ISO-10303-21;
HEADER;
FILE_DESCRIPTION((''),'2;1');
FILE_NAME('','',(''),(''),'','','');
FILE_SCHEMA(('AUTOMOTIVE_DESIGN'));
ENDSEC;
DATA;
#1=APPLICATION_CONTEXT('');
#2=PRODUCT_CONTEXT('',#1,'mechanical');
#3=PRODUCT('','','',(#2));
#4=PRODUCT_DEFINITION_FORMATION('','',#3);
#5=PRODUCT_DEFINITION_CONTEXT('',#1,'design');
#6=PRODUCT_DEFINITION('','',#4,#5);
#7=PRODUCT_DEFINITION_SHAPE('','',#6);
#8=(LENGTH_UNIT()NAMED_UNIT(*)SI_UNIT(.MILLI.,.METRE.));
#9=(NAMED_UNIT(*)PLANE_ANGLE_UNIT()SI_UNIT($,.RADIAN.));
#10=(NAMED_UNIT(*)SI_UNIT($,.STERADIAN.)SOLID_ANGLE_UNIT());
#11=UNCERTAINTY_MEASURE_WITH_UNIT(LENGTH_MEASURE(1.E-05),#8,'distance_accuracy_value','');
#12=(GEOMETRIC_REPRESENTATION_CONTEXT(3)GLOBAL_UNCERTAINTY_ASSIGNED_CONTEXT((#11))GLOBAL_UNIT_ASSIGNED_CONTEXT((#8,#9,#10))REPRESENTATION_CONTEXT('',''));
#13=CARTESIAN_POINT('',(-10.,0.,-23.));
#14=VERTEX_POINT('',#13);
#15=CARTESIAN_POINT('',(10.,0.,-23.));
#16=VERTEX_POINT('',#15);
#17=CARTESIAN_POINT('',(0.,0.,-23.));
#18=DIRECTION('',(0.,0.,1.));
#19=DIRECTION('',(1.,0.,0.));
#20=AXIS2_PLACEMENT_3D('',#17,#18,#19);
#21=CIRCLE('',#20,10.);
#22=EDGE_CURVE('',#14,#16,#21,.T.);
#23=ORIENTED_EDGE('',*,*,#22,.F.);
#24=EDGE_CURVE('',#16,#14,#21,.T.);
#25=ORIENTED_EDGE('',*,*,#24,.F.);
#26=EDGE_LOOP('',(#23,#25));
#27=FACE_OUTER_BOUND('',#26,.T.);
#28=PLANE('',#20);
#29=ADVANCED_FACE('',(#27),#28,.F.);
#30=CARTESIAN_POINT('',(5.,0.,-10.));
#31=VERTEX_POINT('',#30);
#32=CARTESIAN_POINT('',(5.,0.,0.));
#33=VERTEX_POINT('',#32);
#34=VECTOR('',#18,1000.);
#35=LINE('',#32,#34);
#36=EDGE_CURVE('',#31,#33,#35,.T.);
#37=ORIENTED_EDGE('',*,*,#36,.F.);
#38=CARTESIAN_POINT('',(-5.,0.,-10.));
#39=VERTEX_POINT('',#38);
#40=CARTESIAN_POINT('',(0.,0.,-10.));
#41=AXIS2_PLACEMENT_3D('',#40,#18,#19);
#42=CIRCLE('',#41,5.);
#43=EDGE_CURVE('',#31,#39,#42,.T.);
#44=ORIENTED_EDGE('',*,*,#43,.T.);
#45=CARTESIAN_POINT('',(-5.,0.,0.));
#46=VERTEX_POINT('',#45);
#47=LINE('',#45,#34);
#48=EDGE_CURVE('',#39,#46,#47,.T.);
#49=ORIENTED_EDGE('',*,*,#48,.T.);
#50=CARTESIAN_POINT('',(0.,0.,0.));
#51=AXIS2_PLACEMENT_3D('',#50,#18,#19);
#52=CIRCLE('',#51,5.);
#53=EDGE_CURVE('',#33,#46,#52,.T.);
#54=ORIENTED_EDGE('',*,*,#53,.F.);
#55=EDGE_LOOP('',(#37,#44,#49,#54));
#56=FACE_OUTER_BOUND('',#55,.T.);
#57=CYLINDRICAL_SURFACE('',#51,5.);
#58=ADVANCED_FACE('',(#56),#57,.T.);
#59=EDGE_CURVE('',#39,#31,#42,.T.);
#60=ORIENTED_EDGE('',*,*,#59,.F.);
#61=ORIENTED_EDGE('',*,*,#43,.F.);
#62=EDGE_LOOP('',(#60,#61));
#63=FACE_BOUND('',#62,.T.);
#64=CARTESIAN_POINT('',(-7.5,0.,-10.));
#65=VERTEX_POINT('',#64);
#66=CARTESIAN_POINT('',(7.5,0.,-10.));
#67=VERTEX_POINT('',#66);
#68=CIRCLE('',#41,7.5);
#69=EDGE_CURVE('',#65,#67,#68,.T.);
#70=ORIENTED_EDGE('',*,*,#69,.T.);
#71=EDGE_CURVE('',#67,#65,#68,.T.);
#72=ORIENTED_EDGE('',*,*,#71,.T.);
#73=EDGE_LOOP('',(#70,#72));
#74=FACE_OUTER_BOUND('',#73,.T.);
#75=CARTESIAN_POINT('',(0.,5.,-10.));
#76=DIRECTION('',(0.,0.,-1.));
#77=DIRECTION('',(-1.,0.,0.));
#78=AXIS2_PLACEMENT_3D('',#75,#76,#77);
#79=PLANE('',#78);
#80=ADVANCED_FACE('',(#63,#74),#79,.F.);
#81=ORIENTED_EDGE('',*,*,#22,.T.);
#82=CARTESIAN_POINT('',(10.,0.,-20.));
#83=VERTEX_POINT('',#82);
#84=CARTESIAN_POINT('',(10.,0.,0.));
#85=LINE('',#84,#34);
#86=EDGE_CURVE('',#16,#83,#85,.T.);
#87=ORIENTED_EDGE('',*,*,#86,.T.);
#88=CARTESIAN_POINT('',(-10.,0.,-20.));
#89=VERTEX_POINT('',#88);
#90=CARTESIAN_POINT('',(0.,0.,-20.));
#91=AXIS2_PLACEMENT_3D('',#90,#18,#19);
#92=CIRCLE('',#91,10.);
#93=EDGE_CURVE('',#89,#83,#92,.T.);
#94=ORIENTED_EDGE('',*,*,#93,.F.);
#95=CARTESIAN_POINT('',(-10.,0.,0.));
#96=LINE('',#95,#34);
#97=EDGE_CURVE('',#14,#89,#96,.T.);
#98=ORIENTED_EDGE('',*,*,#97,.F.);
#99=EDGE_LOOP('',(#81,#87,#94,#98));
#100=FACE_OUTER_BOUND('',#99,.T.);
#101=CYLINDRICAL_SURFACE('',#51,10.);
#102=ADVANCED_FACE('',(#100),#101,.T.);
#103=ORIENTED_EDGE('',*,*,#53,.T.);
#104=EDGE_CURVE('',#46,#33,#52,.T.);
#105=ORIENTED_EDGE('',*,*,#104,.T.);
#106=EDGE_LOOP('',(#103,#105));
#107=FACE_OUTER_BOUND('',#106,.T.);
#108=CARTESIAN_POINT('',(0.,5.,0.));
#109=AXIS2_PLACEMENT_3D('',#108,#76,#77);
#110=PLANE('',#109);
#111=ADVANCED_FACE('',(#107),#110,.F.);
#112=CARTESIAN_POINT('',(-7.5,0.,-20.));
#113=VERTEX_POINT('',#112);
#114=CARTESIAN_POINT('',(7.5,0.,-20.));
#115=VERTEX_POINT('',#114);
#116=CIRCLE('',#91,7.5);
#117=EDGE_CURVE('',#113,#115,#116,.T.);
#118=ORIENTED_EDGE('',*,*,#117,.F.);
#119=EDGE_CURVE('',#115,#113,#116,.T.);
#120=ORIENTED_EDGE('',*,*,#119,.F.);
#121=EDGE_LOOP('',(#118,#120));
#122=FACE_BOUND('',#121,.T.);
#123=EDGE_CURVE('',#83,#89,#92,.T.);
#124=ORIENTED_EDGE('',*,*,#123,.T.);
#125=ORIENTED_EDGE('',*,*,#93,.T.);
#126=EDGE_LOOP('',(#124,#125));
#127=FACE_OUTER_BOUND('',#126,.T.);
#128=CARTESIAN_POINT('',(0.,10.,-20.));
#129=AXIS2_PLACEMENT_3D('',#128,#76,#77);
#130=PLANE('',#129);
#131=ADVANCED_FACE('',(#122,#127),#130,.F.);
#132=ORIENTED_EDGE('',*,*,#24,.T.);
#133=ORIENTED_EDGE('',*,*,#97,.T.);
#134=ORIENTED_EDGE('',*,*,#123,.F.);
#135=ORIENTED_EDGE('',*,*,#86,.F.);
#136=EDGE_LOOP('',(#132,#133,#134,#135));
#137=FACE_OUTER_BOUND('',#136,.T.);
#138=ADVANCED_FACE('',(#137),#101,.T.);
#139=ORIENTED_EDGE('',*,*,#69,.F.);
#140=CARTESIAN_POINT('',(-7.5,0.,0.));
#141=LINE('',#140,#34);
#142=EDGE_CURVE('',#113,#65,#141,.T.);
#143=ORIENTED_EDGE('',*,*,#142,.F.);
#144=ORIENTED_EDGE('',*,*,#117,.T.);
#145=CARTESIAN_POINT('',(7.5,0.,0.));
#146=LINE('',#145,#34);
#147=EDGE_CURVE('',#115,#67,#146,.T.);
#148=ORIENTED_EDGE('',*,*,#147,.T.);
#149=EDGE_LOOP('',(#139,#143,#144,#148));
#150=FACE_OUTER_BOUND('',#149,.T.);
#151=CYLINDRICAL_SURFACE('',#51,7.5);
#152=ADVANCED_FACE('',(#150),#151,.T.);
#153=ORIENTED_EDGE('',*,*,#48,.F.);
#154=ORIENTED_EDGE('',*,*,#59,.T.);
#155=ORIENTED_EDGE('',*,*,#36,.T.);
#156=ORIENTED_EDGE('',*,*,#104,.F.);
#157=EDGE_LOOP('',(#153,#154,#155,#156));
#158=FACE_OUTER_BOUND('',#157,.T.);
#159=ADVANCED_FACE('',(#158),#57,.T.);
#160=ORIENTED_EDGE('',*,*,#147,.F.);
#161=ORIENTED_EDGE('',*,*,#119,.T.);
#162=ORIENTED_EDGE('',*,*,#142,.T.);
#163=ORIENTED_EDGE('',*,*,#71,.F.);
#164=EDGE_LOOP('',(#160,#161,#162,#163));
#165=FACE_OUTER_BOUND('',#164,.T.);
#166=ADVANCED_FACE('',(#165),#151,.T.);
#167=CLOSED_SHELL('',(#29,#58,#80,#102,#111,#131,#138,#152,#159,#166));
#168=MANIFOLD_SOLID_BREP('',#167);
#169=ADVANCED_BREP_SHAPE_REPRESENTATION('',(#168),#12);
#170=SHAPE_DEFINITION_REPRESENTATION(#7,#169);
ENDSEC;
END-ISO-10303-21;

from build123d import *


with BuildPart() as part:
    # Sketch1 → Revolve1 (revolve)
    with BuildSketch(Plane(origin=(0, 0, 0), x_dir=(0, 0, -1), z_dir=(1, 0, 0)), mode=Mode.PRIVATE) as revolve1_sk:
        Polygon((23, 0), (23, 10), (20, 10), (20, 7.5), (10, 7.5), (10, 5), (0, 5), (0, 0), align=None)
    revolve(revolve1_sk.sketch.rotate(Axis((0, 0, 0), (0, 0, -1)), 90), axis=Axis((0, 0, 0), (0, 0, -1)))


solid = part.part
